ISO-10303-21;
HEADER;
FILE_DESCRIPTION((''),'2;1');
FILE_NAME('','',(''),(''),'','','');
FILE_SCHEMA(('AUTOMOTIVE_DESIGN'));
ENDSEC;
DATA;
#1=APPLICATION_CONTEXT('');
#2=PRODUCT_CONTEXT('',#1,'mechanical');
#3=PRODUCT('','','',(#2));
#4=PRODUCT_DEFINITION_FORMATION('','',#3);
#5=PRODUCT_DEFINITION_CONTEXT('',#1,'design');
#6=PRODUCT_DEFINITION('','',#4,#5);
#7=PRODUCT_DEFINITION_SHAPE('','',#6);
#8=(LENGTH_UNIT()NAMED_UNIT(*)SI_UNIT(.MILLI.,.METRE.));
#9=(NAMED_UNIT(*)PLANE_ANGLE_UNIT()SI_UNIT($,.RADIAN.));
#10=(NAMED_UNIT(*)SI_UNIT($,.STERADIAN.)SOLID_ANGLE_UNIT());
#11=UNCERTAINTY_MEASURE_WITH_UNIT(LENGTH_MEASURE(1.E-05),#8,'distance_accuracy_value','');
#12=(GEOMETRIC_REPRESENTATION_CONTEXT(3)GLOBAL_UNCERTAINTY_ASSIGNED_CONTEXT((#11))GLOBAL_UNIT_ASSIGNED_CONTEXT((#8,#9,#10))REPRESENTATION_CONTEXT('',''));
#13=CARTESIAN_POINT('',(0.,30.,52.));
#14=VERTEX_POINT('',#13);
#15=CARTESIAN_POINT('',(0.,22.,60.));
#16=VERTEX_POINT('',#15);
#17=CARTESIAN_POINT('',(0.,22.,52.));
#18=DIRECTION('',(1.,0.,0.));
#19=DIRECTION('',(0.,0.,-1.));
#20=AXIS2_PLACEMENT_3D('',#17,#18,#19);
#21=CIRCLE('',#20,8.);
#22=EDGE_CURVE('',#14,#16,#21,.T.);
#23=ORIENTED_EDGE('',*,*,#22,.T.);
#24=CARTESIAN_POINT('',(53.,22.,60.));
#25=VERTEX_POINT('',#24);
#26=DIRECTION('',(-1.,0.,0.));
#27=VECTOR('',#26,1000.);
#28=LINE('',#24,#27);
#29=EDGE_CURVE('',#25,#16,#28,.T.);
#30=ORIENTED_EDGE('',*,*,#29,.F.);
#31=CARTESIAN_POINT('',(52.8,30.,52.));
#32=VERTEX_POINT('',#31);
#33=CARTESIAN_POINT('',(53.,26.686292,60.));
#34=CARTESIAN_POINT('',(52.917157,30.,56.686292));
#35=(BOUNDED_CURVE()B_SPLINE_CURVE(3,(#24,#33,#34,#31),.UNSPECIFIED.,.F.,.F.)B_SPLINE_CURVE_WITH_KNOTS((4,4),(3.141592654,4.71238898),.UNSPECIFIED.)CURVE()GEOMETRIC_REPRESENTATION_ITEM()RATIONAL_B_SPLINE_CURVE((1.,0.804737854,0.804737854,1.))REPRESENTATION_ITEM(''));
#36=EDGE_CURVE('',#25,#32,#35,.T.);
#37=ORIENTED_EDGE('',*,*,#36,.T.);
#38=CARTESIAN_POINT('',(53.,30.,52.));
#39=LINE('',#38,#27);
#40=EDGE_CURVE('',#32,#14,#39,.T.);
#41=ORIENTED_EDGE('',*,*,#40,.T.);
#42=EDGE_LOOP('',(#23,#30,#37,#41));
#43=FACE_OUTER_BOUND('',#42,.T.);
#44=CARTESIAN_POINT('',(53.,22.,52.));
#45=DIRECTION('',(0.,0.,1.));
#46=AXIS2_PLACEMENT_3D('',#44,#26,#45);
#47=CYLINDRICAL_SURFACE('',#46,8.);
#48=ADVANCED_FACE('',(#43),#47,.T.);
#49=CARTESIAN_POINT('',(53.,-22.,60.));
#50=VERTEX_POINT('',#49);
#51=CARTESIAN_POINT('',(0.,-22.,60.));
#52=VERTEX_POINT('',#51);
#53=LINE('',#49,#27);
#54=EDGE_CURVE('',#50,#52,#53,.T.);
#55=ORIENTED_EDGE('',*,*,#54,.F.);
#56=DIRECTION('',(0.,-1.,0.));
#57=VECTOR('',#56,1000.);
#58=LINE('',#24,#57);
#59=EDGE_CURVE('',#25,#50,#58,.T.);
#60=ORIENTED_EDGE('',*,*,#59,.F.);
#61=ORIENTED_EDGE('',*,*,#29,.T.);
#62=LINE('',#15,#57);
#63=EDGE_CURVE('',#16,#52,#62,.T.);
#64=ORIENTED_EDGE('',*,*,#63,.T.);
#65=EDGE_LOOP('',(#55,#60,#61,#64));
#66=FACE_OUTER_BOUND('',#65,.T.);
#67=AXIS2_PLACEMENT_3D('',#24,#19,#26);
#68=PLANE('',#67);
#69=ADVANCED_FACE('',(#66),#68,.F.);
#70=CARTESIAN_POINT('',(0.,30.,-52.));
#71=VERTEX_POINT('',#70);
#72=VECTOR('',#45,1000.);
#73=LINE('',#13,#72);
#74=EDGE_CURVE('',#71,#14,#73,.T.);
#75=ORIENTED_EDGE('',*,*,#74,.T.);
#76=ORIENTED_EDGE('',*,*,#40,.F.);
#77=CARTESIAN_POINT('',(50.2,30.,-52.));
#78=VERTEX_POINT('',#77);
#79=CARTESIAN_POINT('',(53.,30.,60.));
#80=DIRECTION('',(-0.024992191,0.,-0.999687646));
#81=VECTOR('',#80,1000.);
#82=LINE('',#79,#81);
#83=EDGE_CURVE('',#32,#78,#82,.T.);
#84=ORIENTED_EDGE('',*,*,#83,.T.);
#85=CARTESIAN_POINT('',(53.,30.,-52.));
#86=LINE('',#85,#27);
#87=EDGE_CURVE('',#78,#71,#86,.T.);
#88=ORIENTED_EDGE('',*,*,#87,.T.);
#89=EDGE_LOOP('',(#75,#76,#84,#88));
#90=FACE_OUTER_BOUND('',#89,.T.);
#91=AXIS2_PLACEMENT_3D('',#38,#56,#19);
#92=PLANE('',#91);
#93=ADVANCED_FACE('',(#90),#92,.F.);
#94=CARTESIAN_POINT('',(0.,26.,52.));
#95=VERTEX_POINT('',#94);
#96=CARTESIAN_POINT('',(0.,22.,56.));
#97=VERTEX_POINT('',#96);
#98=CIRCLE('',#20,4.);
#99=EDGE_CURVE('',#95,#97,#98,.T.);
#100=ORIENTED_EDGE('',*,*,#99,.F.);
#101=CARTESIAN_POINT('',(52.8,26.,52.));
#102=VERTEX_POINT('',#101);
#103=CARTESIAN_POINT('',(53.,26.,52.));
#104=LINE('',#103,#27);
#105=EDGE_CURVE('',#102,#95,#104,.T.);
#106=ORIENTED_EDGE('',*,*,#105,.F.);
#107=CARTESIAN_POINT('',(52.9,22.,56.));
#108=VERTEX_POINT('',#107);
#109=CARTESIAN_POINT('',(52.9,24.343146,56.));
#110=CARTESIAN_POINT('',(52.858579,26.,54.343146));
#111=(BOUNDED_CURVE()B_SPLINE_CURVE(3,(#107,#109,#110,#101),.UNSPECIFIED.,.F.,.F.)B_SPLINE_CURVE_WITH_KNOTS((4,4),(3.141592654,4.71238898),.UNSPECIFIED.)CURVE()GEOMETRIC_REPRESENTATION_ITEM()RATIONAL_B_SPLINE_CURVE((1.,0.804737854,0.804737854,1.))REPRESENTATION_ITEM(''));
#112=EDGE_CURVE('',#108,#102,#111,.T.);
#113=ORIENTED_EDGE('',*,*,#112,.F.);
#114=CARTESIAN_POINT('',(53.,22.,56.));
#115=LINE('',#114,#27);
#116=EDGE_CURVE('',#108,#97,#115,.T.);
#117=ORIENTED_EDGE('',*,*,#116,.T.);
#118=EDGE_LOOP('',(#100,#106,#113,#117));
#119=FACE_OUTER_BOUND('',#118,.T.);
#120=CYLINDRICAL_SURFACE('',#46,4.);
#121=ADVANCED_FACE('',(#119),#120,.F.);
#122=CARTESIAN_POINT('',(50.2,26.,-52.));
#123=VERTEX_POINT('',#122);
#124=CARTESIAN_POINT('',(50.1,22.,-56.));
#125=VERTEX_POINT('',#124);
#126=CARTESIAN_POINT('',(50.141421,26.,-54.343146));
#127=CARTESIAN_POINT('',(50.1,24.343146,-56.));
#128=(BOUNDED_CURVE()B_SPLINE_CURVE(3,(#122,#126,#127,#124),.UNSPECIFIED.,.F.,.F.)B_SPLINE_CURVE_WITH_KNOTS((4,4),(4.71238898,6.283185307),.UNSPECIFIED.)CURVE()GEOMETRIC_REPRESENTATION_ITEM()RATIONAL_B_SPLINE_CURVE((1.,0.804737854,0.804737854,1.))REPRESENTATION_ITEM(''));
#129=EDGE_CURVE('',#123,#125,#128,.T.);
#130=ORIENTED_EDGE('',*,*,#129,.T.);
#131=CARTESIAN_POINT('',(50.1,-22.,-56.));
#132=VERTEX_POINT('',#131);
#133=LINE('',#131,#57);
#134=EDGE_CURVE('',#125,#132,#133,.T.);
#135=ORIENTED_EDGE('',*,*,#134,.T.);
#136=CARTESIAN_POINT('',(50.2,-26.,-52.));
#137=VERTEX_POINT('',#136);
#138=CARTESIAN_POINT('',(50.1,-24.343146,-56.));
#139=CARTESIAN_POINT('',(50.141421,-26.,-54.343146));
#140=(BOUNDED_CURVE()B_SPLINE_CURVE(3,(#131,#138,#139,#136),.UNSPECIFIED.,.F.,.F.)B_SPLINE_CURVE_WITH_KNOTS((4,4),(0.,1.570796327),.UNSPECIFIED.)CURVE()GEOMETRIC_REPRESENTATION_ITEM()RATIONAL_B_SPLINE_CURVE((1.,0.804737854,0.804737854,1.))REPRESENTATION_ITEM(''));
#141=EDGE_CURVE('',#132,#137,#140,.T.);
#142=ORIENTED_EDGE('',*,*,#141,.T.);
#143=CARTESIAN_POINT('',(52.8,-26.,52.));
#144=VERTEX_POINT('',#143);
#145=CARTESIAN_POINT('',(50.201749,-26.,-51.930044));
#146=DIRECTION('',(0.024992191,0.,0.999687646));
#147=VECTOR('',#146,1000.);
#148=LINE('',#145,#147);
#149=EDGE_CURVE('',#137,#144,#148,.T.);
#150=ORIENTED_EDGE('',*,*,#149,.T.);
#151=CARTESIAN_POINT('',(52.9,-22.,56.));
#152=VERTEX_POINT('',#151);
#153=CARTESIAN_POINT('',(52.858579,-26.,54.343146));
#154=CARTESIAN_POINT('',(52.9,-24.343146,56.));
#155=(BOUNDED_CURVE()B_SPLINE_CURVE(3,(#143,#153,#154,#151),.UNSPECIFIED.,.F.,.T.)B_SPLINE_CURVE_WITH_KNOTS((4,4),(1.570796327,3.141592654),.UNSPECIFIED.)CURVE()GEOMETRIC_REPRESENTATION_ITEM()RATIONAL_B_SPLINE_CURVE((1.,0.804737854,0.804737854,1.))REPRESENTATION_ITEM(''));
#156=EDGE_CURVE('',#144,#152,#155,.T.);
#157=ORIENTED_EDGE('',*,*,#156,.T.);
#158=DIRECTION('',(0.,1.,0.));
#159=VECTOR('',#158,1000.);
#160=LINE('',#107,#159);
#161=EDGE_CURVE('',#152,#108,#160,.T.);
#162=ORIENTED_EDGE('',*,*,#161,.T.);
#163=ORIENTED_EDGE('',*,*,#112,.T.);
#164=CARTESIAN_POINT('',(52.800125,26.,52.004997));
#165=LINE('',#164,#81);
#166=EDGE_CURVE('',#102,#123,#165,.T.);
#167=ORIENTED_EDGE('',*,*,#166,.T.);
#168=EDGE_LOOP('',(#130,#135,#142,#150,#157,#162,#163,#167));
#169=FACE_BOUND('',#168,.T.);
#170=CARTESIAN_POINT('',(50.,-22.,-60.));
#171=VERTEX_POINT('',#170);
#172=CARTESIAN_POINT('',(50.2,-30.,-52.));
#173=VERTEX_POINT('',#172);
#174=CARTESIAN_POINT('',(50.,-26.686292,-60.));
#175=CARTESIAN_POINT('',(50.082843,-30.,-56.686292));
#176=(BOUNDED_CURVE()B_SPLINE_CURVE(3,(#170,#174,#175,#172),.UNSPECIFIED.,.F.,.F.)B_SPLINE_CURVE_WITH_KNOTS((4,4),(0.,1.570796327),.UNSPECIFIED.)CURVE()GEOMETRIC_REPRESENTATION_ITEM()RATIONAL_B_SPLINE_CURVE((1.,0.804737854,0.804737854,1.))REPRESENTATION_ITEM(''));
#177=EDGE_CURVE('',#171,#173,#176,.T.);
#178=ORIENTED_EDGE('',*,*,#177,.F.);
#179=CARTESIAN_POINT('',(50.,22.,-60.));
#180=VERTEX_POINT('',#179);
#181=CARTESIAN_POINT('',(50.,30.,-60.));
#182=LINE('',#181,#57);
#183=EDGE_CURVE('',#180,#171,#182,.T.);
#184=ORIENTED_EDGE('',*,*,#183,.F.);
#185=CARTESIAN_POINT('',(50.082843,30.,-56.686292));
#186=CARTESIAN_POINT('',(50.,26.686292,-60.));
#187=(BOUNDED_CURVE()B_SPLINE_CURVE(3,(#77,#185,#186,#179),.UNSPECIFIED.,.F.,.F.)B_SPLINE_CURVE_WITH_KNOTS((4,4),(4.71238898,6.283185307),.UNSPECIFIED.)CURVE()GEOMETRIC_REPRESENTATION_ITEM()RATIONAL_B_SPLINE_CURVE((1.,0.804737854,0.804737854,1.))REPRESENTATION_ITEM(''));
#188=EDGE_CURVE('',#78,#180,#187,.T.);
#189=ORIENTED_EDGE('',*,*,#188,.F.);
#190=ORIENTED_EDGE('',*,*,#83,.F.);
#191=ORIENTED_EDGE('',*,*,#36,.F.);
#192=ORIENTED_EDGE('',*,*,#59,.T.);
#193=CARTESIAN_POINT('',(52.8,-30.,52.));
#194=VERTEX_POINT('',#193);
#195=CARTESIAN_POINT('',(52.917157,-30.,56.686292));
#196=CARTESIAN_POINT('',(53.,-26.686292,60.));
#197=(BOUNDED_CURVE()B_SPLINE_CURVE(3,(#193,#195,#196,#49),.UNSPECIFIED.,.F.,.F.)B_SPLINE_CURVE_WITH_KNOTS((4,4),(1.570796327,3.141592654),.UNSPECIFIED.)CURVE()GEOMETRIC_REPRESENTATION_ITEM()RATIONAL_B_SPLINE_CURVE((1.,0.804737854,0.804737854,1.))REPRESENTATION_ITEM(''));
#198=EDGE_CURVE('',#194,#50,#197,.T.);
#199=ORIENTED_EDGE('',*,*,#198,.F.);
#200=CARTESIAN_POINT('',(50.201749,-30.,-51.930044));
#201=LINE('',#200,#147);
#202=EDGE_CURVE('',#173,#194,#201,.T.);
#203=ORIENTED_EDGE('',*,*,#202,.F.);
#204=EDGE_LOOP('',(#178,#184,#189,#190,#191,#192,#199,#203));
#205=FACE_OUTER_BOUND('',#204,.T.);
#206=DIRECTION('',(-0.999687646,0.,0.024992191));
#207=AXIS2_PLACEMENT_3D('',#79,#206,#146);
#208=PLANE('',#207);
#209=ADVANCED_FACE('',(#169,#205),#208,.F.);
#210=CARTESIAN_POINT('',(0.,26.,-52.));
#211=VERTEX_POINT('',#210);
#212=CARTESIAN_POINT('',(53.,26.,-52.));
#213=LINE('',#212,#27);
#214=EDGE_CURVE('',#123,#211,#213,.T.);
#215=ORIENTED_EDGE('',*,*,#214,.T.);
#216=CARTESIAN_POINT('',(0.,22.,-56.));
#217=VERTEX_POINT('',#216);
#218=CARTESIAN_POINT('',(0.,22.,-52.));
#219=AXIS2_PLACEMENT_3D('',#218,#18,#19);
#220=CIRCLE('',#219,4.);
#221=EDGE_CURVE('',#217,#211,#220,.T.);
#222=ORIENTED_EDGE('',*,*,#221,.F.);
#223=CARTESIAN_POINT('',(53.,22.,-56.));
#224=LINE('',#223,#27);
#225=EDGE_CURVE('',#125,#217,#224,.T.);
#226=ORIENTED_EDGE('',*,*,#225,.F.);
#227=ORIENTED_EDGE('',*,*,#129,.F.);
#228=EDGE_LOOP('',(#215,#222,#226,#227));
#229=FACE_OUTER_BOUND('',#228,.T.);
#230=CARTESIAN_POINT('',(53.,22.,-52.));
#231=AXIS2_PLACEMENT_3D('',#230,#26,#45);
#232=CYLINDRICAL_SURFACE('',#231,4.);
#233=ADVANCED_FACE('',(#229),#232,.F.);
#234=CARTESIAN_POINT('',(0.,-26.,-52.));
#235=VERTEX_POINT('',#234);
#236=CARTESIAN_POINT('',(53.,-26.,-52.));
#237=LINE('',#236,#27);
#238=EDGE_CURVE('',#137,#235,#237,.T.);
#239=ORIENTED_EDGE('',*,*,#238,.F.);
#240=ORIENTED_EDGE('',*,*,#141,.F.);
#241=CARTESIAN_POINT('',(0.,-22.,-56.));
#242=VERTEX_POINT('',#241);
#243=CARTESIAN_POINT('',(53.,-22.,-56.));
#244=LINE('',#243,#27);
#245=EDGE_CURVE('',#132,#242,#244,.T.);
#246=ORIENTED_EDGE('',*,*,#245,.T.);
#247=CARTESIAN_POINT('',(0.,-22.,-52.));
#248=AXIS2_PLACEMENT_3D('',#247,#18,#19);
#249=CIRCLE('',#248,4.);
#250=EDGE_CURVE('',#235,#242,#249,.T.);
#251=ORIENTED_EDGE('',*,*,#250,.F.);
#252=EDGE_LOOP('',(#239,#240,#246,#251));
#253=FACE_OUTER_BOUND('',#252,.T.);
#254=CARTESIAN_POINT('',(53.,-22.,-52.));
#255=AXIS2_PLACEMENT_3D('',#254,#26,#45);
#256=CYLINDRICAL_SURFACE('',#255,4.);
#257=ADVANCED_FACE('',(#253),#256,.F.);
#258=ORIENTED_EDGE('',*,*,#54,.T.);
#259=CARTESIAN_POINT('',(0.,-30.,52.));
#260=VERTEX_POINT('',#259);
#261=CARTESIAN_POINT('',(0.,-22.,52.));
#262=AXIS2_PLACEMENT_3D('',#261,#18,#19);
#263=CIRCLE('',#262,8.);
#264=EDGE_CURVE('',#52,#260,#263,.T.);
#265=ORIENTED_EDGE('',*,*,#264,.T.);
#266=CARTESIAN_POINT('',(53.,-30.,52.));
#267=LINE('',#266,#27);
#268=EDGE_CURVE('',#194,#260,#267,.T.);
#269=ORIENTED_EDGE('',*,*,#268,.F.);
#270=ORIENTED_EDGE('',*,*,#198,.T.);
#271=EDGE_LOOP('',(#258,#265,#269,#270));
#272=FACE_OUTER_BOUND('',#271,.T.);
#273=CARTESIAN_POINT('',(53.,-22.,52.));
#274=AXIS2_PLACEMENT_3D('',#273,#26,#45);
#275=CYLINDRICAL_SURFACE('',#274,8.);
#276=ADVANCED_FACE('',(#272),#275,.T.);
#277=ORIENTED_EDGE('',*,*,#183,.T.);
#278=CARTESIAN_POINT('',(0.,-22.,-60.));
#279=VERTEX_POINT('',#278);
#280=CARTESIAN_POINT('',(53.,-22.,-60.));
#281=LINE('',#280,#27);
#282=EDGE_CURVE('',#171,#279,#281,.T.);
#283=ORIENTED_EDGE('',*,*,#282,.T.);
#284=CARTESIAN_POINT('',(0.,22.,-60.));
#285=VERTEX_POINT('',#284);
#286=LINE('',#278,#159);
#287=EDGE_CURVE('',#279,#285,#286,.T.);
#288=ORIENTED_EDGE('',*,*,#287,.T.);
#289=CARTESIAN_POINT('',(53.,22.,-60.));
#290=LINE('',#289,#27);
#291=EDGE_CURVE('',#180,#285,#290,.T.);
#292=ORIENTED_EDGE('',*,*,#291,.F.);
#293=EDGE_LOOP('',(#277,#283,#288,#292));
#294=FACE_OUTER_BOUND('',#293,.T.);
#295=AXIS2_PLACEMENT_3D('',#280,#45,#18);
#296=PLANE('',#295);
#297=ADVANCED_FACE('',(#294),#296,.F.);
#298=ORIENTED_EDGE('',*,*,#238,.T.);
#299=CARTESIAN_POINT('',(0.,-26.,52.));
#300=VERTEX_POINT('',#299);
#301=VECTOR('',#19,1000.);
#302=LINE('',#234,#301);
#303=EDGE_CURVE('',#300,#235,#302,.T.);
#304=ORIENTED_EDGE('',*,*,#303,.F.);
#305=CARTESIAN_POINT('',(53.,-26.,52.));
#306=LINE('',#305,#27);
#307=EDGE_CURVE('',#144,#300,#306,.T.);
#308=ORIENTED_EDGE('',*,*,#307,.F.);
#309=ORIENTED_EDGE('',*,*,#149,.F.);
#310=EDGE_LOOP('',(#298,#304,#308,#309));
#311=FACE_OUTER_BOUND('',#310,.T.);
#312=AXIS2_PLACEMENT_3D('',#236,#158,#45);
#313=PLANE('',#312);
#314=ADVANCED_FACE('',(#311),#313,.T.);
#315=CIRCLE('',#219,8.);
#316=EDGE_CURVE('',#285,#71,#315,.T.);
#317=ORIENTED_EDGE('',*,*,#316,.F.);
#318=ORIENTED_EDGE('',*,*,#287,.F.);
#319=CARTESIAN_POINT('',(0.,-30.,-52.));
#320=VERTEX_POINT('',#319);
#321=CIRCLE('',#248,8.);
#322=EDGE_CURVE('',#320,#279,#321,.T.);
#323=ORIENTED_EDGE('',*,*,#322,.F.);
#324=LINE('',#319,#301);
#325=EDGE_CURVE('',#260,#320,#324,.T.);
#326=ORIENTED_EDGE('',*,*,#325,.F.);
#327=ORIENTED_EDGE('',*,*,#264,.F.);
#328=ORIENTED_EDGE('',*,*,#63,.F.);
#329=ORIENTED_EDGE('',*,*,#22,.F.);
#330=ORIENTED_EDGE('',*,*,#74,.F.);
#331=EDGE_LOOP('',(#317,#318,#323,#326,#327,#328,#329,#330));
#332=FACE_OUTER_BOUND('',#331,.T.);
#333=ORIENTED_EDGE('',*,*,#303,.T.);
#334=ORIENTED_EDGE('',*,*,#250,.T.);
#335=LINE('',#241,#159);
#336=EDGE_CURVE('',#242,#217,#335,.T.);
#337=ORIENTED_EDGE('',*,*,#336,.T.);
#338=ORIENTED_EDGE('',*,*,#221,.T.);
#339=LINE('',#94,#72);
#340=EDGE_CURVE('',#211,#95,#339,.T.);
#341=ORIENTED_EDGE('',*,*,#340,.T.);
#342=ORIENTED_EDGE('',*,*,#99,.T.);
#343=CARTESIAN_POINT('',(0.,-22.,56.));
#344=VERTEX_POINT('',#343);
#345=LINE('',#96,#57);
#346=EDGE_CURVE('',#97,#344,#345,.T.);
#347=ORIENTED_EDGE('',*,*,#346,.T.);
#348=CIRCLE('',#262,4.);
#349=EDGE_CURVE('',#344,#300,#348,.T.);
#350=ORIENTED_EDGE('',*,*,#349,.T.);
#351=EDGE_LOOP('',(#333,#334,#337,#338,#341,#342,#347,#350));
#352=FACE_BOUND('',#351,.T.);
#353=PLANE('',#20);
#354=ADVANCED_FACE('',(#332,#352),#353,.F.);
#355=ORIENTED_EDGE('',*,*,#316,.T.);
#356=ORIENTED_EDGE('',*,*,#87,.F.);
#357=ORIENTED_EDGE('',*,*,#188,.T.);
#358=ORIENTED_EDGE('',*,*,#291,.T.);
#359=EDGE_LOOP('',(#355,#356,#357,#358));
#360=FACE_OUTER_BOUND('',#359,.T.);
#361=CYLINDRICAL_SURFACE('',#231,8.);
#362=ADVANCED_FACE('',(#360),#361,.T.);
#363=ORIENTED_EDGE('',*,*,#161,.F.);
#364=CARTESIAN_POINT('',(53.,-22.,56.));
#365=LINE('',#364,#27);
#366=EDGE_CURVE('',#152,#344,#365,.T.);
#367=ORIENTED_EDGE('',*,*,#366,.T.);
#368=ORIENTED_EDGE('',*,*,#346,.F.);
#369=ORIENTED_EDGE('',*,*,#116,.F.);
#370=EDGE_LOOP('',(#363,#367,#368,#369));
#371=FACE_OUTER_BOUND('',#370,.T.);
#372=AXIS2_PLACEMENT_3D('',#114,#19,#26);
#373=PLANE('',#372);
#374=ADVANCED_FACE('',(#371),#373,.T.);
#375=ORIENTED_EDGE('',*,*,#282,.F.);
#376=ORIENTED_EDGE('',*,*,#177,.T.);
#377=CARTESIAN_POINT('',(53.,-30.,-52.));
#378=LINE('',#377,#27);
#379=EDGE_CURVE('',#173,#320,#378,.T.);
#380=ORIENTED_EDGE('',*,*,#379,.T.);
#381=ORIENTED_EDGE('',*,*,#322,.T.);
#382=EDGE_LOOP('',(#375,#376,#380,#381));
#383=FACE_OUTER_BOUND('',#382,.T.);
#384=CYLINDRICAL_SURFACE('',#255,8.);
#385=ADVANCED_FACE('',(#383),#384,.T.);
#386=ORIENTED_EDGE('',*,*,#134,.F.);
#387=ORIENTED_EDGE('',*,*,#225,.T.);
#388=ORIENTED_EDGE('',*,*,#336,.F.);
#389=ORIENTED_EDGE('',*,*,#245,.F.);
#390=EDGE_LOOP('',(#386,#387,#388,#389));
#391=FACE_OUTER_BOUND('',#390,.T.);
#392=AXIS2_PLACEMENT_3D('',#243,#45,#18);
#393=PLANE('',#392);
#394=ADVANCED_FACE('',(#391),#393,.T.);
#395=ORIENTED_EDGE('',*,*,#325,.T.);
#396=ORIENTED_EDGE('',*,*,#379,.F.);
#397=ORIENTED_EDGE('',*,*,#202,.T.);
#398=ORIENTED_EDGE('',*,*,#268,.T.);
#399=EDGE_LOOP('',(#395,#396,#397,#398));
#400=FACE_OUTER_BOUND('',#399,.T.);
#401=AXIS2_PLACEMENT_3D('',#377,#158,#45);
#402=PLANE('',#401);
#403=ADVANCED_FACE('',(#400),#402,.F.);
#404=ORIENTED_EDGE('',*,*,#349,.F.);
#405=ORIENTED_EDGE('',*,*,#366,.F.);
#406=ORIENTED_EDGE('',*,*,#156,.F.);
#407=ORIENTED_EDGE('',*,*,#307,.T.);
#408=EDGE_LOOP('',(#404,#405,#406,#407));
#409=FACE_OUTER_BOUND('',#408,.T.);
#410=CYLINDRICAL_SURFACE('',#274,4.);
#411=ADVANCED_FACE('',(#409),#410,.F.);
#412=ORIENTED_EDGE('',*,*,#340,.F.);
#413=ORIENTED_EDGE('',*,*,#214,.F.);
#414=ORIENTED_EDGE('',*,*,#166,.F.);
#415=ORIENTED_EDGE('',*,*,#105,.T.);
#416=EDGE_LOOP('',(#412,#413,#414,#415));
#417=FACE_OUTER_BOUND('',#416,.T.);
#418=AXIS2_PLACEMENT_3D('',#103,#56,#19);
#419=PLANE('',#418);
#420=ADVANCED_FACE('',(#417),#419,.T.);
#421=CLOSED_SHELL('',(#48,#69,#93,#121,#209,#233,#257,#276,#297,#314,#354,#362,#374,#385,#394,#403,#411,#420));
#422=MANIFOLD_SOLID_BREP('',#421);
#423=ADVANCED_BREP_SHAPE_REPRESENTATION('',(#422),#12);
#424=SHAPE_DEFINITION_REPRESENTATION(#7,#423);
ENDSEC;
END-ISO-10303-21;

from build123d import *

# Parameters (mm, degrees)
GB_6728_1986_RECTANGULAR_HOLLOW_SECTION_DEPTH = 53
CUT_EXTRUDE1_DEPTH                            = 101.04498988
CUT_EXTRUDE1_DEPTH_BACK                       = 101.04498988


with BuildPart() as part:
    # Sketch1 → GB/6728-1986 rectangular hollow section 120 X 60 X 4(1) (new body)
    with BuildSketch(Plane.YZ):
        with BuildLine():
            Line((-22, -60), (22, -60))
            ThreePointArc((22, -60), (27.656854249, -57.656854249), (30, -52))
            Line((30, -52), (30, 52))
            ThreePointArc((30, 52), (27.656854249, 57.656854249), (22, 60))
            Line((22, 60), (-22, 60))
            ThreePointArc((-22, 60), (-27.656854249, 57.656854249), (-30, 52))
            Line((-30, 52), (-30, -52))
            ThreePointArc((-30, -52), (-27.656854249, -57.656854249), (-22, -60))
        make_face()
        with BuildLine():
            Line((-22, -56), (22, -56))
            ThreePointArc((22, -56), (24.828427125, -54.828427125), (26, -52))
            Line((26, -52), (26, 52))
            ThreePointArc((26, 52), (24.828427125, 54.828427125), (22, 56))
            Line((22, 56), (-22, 56))
            ThreePointArc((-22, 56), (-24.828427125, 54.828427125), (-26, 52))
            Line((-26, 52), (-26, -52))
            ThreePointArc((-26, -52), (-24.828427125, -54.828427125), (-22, -56))
        make_face(mode=Mode.SUBTRACT)
    extrude(amount=GB_6728_1986_RECTANGULAR_HOLLOW_SECTION_DEPTH)

    # Sketch3 → Cut-Extrude1 (cut, two sides: drawn at the far end of the back side and taken through both)
    with BuildSketch(Plane.XZ.offset(30).offset(-CUT_EXTRUDE1_DEPTH_BACK)):
        Polygon((53, 60), (50, -60), (53, -60), align=None)
    extrude(amount=CUT_EXTRUDE1_DEPTH + CUT_EXTRUDE1_DEPTH_BACK, mode=Mode.SUBTRACT)


solid = part.part
